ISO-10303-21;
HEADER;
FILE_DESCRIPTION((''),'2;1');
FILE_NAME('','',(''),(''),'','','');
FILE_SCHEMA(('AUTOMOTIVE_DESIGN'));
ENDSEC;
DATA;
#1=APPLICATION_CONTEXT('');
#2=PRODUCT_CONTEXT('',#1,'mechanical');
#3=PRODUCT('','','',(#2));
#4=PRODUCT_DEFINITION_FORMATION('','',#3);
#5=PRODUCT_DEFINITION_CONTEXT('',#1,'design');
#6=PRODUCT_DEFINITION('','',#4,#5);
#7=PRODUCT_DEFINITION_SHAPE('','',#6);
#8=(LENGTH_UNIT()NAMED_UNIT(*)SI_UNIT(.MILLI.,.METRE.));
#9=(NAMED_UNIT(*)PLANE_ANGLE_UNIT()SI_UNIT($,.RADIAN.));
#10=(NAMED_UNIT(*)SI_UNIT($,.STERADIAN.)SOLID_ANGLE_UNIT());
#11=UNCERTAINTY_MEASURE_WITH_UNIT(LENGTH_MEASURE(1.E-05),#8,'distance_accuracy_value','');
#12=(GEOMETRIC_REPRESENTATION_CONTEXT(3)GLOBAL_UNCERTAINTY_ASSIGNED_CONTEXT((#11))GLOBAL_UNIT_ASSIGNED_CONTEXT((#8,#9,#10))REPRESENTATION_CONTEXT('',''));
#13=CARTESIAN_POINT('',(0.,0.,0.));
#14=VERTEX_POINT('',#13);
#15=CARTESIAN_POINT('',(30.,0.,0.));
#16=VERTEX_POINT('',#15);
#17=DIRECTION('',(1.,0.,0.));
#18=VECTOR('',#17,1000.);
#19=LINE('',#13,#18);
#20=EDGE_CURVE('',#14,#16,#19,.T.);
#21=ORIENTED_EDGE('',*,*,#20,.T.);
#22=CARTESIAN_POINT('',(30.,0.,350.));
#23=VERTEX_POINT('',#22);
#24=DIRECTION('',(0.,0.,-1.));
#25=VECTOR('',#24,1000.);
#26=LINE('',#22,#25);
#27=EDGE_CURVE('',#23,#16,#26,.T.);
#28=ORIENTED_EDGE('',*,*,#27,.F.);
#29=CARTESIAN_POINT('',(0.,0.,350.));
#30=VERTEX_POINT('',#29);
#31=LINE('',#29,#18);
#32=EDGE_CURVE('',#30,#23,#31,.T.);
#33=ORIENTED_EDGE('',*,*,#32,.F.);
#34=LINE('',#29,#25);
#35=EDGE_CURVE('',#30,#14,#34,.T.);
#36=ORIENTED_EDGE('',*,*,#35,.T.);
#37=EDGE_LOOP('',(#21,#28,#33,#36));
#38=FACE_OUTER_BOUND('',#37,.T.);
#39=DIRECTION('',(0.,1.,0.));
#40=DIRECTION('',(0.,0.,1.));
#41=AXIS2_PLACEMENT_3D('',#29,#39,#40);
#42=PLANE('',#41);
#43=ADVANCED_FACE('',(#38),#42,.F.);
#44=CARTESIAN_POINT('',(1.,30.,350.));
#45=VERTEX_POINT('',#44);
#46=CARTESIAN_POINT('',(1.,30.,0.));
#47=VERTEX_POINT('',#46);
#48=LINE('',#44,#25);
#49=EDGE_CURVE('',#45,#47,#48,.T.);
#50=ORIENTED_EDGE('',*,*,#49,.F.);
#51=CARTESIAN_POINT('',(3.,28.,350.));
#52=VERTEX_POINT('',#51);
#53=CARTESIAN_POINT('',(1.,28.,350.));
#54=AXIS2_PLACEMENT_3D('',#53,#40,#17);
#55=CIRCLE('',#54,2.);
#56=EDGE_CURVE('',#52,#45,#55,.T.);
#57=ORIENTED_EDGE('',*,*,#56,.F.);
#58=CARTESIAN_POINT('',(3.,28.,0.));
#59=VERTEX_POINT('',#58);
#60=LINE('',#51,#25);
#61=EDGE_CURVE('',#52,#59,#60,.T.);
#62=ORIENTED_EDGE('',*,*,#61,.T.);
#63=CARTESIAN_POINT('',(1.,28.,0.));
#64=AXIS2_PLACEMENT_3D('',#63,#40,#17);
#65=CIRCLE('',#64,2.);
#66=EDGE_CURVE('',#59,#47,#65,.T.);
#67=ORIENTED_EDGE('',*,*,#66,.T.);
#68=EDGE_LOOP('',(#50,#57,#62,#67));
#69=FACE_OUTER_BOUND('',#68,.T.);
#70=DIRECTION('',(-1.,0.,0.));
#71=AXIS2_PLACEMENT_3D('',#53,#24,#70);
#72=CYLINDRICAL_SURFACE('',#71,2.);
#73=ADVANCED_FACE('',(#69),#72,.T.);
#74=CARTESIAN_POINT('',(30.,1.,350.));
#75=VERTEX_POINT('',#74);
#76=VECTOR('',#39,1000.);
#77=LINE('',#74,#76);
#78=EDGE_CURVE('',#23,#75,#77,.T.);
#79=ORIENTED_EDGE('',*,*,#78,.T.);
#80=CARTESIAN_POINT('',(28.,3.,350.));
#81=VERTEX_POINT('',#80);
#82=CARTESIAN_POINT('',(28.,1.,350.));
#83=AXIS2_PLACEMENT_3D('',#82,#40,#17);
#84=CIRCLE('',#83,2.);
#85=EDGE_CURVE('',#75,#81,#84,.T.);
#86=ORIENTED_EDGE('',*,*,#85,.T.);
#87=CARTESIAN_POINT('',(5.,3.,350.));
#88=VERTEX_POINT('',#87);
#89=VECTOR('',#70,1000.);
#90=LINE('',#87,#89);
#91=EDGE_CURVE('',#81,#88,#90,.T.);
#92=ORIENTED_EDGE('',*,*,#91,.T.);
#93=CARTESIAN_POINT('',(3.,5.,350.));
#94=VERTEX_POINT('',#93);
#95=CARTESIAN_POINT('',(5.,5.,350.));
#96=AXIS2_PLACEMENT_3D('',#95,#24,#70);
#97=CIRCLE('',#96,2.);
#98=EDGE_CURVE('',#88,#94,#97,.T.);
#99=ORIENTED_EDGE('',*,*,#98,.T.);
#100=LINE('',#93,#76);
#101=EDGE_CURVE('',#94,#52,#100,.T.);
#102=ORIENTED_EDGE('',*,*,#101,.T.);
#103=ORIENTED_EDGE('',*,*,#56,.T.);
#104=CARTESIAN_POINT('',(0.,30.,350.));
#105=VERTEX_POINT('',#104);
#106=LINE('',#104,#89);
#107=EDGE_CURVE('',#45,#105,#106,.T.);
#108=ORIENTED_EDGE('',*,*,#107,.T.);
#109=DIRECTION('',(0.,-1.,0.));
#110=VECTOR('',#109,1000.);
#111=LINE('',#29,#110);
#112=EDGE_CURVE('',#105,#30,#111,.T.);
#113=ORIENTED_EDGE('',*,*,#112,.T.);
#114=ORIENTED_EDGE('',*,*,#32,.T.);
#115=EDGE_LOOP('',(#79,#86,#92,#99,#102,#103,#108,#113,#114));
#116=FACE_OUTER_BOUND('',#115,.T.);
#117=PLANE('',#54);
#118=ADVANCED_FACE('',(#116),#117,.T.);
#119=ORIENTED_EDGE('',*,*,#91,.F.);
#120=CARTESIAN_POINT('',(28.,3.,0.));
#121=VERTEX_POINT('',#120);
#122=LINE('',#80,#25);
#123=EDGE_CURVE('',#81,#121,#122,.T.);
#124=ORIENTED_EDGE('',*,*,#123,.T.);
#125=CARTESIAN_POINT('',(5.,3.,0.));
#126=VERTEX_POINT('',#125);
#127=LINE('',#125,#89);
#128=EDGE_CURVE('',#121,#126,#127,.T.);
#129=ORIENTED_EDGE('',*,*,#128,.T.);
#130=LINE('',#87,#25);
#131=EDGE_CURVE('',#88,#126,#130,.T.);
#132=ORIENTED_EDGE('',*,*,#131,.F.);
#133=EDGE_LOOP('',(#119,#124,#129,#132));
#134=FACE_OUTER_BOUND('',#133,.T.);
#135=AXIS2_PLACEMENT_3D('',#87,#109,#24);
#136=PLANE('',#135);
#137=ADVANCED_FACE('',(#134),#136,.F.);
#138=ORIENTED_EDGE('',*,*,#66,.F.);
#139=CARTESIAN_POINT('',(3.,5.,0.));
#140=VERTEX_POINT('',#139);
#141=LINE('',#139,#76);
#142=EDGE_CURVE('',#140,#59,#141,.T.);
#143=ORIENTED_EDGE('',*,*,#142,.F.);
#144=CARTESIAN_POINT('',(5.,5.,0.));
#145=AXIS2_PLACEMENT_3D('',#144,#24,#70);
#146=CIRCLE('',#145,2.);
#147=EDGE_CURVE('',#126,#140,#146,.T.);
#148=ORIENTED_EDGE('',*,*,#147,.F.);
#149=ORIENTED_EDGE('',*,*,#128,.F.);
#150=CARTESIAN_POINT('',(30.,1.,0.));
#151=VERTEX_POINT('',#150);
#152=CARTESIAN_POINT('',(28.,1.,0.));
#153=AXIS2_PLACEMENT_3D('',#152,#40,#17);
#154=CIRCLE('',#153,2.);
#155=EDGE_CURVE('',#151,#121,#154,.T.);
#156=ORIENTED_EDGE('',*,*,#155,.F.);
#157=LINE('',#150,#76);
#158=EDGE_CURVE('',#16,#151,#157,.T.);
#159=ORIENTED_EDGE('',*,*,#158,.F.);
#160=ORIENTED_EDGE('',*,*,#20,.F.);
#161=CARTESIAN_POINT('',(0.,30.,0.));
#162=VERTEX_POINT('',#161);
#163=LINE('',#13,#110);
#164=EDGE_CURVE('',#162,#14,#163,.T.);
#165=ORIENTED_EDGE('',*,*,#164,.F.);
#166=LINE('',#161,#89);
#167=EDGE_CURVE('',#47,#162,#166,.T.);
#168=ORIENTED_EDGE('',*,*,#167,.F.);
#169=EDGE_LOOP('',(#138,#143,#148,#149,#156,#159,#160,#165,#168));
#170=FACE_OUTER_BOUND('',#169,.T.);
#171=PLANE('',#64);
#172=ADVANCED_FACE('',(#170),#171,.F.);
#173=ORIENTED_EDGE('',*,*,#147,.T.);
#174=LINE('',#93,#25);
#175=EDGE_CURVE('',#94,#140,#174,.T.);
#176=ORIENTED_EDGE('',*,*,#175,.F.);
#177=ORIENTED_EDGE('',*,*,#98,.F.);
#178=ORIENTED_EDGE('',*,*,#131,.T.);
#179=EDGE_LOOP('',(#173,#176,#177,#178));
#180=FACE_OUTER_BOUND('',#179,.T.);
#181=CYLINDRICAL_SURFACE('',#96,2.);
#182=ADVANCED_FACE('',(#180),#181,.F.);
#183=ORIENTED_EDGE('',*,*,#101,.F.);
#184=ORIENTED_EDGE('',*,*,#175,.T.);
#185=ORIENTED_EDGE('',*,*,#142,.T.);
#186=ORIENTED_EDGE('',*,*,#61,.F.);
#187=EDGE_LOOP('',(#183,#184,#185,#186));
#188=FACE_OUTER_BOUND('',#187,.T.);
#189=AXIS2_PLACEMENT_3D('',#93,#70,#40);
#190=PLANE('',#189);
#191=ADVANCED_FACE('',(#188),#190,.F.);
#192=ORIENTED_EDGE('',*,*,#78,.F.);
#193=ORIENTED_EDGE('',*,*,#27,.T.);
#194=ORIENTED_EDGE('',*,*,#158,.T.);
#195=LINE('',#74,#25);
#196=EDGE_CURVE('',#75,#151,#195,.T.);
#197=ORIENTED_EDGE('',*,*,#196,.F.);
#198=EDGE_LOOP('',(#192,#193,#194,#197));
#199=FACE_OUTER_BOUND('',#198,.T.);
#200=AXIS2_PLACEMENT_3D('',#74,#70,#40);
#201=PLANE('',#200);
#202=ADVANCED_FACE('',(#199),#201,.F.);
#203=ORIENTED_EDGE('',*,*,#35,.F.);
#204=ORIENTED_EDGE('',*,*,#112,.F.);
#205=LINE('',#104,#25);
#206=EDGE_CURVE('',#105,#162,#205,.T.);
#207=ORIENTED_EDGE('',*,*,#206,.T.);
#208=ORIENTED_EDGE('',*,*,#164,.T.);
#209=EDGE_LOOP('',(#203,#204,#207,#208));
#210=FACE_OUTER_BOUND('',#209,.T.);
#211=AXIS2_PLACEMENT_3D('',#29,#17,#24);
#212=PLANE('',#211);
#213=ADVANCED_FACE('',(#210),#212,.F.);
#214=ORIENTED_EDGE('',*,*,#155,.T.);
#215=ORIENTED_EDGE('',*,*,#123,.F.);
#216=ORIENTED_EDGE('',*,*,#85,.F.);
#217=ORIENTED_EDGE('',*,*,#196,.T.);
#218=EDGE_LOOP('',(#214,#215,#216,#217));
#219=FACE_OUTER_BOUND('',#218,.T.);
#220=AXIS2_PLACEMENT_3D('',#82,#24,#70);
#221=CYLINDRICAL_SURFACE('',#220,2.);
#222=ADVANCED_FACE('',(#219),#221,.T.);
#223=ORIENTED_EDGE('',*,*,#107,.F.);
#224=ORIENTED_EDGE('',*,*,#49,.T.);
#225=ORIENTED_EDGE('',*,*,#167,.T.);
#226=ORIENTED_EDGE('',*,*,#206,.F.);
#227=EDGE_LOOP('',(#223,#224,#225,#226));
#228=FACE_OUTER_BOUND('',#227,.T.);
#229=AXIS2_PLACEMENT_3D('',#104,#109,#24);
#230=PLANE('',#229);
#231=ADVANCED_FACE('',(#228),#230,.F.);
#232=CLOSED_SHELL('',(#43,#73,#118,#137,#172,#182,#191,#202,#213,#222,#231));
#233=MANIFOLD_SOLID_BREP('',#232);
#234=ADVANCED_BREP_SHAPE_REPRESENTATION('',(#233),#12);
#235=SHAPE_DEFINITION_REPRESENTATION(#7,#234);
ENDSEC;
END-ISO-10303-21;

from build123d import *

# Parameters (mm, degrees)
BOSS_EXTRUDE1_DEPTH = 350


with BuildPart() as part:
    # Sketch1 → Boss-Extrude1 (new body)
    with BuildSketch(Plane.XY):
        with BuildLine():
            Line((0, 0), (30, 0))
            Line((30, 0), (30, 1))
            ThreePointArc((30, 1), (29.414213562, 2.414213562), (28, 3))
            Line((28, 3), (5, 3))
            ThreePointArc((5, 3), (3.585786438, 3.585786438), (3, 5))
            Line((3, 5), (3, 28))
            ThreePointArc((3, 28), (2.414213562, 29.414213562), (1, 30))
            Line((1, 30), (0, 30))
            Line((0, 30), (0, 0))
        make_face()
    extrude(amount=BOSS_EXTRUDE1_DEPTH)


solid = part.part
